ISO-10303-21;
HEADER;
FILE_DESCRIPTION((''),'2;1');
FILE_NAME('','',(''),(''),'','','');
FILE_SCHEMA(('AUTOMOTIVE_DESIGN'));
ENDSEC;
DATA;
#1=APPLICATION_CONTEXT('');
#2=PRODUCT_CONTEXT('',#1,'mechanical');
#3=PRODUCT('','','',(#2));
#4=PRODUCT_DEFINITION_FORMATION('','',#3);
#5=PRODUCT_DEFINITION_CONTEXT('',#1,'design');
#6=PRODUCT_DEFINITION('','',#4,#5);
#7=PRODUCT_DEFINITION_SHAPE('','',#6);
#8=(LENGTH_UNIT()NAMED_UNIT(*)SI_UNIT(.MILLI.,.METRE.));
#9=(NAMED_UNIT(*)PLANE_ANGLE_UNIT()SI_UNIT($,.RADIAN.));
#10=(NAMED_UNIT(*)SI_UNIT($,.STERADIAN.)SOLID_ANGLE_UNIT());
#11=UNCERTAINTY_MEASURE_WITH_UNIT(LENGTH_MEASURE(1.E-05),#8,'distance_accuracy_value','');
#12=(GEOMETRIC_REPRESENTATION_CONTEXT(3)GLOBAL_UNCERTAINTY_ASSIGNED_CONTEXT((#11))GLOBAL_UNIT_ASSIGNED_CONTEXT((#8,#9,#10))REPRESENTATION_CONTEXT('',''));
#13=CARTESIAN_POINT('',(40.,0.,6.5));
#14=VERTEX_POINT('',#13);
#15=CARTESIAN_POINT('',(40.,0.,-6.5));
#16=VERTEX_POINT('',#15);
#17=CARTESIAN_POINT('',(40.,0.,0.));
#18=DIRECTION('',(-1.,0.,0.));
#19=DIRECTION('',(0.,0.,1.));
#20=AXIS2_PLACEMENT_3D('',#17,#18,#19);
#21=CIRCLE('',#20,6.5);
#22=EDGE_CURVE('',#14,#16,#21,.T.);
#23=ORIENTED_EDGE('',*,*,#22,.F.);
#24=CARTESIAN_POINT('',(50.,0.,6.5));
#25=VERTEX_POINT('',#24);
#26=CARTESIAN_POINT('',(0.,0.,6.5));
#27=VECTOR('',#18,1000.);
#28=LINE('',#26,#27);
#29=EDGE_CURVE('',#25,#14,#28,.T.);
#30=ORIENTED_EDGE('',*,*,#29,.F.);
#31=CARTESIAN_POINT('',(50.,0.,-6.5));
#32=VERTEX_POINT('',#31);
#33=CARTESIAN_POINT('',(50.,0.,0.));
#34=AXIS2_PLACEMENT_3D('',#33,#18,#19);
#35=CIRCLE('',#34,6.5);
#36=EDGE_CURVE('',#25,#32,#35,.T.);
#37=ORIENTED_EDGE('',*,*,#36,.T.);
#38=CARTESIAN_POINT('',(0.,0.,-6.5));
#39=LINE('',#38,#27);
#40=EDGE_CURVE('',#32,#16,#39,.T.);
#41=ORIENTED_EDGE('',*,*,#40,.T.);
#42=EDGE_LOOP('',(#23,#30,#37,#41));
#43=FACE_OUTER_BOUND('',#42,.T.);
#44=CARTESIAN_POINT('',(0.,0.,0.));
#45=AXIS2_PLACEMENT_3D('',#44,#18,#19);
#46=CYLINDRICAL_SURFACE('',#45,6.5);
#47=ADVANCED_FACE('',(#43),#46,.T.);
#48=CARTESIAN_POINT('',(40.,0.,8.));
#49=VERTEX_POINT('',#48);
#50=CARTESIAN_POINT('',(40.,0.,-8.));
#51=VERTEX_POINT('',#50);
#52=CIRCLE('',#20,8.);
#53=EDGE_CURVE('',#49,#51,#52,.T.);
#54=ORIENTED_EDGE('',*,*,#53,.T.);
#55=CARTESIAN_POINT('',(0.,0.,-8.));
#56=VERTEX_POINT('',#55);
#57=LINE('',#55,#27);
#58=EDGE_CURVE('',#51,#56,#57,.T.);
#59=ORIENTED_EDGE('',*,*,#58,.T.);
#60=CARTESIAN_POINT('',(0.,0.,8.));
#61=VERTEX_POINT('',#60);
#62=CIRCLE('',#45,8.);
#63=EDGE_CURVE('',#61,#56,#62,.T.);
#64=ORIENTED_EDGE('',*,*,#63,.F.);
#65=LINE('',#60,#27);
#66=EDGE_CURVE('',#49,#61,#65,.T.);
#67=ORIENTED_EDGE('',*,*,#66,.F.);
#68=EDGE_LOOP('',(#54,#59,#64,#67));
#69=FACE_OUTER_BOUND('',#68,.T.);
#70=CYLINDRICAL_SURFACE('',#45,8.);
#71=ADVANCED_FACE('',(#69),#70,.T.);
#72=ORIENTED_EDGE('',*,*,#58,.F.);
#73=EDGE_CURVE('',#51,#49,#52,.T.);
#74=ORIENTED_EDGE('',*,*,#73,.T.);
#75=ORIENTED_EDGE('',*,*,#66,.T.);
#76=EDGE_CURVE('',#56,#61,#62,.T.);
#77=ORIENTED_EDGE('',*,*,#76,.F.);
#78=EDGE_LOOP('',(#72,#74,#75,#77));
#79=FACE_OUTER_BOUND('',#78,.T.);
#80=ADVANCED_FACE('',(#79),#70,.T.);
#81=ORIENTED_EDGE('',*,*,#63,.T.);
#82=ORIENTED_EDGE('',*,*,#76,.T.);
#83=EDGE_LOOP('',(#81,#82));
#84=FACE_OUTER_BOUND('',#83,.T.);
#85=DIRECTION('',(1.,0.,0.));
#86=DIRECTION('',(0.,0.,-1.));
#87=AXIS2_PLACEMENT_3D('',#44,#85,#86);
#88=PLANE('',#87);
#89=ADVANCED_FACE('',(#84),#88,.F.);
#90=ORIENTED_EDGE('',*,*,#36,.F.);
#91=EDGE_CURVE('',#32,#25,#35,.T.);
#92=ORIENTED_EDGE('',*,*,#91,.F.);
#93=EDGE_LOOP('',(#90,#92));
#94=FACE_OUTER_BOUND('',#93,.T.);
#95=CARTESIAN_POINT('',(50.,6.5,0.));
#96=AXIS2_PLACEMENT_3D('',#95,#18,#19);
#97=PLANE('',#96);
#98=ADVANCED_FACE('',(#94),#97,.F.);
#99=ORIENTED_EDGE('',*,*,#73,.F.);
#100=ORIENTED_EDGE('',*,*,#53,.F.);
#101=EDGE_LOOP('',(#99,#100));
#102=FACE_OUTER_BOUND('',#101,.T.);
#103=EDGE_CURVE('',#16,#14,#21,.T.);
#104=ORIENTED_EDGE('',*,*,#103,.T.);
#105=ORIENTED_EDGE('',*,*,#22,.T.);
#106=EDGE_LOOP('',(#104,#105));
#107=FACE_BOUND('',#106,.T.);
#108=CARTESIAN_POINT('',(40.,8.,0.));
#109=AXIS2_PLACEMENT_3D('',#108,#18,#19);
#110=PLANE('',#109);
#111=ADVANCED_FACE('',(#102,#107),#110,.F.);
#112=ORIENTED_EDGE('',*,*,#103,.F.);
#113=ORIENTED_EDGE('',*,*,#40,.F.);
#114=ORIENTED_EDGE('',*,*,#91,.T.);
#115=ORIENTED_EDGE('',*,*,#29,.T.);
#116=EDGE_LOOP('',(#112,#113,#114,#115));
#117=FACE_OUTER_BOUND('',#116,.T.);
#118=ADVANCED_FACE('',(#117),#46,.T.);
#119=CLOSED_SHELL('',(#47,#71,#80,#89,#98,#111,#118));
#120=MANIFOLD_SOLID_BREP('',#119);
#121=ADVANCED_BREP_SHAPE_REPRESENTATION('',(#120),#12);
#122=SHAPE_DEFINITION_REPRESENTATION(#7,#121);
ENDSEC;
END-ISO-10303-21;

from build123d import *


with BuildPart() as part:
    # Sketch1 → Revolve1 (revolve)
    with BuildSketch(Plane.XY, mode=Mode.PRIVATE) as revolve1_sk:
        Polygon((0, 0), (0, 8), (40, 8), (40, 6.5), (50, 6.5), (50, 0), align=None)
    revolve(revolve1_sk.sketch.rotate(Axis((0, 0, 0), (1, 0, 0)), 90), axis=Axis((0, 0, 0), (1, 0, 0)))


solid = part.part
